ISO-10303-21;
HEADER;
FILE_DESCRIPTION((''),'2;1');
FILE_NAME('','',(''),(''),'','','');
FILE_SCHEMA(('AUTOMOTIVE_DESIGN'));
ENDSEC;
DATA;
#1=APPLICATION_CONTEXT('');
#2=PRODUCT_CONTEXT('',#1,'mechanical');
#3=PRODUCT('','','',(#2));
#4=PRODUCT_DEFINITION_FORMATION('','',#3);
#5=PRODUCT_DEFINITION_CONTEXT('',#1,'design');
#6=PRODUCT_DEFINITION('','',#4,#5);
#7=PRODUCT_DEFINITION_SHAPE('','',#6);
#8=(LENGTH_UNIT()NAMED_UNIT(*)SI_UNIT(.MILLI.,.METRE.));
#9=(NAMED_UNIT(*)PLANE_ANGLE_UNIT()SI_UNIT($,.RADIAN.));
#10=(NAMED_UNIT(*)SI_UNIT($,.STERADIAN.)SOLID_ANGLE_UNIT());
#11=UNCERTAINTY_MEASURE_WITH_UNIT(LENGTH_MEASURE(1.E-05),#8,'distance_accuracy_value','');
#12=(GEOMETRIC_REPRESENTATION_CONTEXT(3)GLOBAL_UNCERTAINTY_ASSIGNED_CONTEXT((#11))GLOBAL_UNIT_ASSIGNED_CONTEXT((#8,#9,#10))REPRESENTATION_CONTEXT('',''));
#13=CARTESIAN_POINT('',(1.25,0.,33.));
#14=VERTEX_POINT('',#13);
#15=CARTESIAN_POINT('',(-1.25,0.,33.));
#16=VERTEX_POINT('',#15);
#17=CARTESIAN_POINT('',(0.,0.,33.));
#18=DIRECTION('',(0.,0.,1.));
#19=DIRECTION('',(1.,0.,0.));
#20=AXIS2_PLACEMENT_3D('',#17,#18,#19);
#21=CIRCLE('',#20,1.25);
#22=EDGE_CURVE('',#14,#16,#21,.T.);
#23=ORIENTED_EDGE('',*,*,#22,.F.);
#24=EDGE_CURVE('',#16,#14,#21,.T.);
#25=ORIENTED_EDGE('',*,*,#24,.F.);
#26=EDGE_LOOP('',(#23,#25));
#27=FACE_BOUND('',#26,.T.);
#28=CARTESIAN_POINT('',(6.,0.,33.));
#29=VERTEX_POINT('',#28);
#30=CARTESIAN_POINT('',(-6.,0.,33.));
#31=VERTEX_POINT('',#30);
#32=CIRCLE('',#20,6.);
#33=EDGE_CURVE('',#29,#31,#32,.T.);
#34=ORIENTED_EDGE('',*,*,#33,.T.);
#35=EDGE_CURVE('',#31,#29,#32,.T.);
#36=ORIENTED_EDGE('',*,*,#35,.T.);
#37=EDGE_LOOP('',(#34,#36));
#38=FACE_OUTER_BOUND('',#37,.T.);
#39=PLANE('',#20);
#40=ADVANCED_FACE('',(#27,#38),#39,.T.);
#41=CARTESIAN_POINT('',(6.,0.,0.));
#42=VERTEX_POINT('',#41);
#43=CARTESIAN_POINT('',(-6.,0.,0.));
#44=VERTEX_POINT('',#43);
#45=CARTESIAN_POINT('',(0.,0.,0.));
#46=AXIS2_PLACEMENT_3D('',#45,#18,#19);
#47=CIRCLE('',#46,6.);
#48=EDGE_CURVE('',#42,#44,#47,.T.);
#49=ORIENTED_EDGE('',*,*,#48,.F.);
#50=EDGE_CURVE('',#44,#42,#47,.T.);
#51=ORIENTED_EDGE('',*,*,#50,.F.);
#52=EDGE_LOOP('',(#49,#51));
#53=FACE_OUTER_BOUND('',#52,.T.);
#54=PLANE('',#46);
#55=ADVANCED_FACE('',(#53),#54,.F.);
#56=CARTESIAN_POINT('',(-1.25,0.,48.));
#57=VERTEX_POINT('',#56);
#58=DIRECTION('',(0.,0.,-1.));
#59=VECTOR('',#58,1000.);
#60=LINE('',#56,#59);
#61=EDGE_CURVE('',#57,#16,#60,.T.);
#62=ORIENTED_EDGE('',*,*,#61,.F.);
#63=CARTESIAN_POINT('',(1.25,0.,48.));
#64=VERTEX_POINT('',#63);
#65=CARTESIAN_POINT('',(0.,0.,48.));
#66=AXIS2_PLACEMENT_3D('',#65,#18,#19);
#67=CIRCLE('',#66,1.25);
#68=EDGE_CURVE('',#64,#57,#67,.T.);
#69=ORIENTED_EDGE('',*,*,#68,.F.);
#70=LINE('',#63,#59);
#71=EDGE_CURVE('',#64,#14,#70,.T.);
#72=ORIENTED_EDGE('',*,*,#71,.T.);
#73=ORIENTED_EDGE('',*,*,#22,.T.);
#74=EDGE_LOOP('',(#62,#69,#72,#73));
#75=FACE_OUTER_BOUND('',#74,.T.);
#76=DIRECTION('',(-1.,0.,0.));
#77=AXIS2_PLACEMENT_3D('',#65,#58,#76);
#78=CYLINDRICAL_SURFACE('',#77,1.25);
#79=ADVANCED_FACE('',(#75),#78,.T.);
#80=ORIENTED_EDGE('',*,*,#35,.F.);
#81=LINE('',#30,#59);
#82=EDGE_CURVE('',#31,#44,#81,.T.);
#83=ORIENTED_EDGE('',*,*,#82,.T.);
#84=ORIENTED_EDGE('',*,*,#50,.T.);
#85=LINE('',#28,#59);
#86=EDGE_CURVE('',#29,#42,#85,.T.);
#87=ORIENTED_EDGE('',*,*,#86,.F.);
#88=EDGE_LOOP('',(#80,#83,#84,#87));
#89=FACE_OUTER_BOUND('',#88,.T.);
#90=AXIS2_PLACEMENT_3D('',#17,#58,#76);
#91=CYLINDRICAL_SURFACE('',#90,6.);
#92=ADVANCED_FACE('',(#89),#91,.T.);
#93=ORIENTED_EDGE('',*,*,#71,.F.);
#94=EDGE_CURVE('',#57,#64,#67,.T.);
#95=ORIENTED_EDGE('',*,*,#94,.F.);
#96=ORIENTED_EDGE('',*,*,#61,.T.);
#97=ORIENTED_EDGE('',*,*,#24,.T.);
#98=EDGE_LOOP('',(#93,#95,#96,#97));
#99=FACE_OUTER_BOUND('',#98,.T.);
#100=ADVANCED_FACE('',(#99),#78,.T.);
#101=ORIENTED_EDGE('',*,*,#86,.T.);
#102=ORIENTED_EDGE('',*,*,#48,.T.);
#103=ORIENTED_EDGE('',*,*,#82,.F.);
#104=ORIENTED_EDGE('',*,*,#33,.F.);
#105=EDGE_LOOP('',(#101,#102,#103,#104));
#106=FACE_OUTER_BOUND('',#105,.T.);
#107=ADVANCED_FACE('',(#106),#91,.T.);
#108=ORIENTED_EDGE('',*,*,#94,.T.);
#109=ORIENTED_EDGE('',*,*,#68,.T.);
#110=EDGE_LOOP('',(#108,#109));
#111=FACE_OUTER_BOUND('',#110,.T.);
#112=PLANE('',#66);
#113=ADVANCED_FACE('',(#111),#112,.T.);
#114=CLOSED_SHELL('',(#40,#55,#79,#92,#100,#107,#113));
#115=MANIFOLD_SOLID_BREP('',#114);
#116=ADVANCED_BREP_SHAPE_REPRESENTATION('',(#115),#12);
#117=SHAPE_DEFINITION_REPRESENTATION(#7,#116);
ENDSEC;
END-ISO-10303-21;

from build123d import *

# Parameters (mm, degrees)
SKETCH_1_R      = 6
EXTRUDE_1_DEPTH = 33
SKETCH_2_R      = 1.25
EXTRUDE_2_DEPTH = 15


with BuildPart() as part:
    # 草图1 → 凸台-拉伸1 (new body)
    with BuildSketch(Plane.XY):
        Circle(SKETCH_1_R)
    extrude(amount=EXTRUDE_1_DEPTH)

    # 草图2 → 凸台-拉伸2 (add)
    with BuildSketch(Plane.XY.offset(33)):
        Circle(SKETCH_2_R)
    extrude(amount=EXTRUDE_2_DEPTH)


solid = part.part
